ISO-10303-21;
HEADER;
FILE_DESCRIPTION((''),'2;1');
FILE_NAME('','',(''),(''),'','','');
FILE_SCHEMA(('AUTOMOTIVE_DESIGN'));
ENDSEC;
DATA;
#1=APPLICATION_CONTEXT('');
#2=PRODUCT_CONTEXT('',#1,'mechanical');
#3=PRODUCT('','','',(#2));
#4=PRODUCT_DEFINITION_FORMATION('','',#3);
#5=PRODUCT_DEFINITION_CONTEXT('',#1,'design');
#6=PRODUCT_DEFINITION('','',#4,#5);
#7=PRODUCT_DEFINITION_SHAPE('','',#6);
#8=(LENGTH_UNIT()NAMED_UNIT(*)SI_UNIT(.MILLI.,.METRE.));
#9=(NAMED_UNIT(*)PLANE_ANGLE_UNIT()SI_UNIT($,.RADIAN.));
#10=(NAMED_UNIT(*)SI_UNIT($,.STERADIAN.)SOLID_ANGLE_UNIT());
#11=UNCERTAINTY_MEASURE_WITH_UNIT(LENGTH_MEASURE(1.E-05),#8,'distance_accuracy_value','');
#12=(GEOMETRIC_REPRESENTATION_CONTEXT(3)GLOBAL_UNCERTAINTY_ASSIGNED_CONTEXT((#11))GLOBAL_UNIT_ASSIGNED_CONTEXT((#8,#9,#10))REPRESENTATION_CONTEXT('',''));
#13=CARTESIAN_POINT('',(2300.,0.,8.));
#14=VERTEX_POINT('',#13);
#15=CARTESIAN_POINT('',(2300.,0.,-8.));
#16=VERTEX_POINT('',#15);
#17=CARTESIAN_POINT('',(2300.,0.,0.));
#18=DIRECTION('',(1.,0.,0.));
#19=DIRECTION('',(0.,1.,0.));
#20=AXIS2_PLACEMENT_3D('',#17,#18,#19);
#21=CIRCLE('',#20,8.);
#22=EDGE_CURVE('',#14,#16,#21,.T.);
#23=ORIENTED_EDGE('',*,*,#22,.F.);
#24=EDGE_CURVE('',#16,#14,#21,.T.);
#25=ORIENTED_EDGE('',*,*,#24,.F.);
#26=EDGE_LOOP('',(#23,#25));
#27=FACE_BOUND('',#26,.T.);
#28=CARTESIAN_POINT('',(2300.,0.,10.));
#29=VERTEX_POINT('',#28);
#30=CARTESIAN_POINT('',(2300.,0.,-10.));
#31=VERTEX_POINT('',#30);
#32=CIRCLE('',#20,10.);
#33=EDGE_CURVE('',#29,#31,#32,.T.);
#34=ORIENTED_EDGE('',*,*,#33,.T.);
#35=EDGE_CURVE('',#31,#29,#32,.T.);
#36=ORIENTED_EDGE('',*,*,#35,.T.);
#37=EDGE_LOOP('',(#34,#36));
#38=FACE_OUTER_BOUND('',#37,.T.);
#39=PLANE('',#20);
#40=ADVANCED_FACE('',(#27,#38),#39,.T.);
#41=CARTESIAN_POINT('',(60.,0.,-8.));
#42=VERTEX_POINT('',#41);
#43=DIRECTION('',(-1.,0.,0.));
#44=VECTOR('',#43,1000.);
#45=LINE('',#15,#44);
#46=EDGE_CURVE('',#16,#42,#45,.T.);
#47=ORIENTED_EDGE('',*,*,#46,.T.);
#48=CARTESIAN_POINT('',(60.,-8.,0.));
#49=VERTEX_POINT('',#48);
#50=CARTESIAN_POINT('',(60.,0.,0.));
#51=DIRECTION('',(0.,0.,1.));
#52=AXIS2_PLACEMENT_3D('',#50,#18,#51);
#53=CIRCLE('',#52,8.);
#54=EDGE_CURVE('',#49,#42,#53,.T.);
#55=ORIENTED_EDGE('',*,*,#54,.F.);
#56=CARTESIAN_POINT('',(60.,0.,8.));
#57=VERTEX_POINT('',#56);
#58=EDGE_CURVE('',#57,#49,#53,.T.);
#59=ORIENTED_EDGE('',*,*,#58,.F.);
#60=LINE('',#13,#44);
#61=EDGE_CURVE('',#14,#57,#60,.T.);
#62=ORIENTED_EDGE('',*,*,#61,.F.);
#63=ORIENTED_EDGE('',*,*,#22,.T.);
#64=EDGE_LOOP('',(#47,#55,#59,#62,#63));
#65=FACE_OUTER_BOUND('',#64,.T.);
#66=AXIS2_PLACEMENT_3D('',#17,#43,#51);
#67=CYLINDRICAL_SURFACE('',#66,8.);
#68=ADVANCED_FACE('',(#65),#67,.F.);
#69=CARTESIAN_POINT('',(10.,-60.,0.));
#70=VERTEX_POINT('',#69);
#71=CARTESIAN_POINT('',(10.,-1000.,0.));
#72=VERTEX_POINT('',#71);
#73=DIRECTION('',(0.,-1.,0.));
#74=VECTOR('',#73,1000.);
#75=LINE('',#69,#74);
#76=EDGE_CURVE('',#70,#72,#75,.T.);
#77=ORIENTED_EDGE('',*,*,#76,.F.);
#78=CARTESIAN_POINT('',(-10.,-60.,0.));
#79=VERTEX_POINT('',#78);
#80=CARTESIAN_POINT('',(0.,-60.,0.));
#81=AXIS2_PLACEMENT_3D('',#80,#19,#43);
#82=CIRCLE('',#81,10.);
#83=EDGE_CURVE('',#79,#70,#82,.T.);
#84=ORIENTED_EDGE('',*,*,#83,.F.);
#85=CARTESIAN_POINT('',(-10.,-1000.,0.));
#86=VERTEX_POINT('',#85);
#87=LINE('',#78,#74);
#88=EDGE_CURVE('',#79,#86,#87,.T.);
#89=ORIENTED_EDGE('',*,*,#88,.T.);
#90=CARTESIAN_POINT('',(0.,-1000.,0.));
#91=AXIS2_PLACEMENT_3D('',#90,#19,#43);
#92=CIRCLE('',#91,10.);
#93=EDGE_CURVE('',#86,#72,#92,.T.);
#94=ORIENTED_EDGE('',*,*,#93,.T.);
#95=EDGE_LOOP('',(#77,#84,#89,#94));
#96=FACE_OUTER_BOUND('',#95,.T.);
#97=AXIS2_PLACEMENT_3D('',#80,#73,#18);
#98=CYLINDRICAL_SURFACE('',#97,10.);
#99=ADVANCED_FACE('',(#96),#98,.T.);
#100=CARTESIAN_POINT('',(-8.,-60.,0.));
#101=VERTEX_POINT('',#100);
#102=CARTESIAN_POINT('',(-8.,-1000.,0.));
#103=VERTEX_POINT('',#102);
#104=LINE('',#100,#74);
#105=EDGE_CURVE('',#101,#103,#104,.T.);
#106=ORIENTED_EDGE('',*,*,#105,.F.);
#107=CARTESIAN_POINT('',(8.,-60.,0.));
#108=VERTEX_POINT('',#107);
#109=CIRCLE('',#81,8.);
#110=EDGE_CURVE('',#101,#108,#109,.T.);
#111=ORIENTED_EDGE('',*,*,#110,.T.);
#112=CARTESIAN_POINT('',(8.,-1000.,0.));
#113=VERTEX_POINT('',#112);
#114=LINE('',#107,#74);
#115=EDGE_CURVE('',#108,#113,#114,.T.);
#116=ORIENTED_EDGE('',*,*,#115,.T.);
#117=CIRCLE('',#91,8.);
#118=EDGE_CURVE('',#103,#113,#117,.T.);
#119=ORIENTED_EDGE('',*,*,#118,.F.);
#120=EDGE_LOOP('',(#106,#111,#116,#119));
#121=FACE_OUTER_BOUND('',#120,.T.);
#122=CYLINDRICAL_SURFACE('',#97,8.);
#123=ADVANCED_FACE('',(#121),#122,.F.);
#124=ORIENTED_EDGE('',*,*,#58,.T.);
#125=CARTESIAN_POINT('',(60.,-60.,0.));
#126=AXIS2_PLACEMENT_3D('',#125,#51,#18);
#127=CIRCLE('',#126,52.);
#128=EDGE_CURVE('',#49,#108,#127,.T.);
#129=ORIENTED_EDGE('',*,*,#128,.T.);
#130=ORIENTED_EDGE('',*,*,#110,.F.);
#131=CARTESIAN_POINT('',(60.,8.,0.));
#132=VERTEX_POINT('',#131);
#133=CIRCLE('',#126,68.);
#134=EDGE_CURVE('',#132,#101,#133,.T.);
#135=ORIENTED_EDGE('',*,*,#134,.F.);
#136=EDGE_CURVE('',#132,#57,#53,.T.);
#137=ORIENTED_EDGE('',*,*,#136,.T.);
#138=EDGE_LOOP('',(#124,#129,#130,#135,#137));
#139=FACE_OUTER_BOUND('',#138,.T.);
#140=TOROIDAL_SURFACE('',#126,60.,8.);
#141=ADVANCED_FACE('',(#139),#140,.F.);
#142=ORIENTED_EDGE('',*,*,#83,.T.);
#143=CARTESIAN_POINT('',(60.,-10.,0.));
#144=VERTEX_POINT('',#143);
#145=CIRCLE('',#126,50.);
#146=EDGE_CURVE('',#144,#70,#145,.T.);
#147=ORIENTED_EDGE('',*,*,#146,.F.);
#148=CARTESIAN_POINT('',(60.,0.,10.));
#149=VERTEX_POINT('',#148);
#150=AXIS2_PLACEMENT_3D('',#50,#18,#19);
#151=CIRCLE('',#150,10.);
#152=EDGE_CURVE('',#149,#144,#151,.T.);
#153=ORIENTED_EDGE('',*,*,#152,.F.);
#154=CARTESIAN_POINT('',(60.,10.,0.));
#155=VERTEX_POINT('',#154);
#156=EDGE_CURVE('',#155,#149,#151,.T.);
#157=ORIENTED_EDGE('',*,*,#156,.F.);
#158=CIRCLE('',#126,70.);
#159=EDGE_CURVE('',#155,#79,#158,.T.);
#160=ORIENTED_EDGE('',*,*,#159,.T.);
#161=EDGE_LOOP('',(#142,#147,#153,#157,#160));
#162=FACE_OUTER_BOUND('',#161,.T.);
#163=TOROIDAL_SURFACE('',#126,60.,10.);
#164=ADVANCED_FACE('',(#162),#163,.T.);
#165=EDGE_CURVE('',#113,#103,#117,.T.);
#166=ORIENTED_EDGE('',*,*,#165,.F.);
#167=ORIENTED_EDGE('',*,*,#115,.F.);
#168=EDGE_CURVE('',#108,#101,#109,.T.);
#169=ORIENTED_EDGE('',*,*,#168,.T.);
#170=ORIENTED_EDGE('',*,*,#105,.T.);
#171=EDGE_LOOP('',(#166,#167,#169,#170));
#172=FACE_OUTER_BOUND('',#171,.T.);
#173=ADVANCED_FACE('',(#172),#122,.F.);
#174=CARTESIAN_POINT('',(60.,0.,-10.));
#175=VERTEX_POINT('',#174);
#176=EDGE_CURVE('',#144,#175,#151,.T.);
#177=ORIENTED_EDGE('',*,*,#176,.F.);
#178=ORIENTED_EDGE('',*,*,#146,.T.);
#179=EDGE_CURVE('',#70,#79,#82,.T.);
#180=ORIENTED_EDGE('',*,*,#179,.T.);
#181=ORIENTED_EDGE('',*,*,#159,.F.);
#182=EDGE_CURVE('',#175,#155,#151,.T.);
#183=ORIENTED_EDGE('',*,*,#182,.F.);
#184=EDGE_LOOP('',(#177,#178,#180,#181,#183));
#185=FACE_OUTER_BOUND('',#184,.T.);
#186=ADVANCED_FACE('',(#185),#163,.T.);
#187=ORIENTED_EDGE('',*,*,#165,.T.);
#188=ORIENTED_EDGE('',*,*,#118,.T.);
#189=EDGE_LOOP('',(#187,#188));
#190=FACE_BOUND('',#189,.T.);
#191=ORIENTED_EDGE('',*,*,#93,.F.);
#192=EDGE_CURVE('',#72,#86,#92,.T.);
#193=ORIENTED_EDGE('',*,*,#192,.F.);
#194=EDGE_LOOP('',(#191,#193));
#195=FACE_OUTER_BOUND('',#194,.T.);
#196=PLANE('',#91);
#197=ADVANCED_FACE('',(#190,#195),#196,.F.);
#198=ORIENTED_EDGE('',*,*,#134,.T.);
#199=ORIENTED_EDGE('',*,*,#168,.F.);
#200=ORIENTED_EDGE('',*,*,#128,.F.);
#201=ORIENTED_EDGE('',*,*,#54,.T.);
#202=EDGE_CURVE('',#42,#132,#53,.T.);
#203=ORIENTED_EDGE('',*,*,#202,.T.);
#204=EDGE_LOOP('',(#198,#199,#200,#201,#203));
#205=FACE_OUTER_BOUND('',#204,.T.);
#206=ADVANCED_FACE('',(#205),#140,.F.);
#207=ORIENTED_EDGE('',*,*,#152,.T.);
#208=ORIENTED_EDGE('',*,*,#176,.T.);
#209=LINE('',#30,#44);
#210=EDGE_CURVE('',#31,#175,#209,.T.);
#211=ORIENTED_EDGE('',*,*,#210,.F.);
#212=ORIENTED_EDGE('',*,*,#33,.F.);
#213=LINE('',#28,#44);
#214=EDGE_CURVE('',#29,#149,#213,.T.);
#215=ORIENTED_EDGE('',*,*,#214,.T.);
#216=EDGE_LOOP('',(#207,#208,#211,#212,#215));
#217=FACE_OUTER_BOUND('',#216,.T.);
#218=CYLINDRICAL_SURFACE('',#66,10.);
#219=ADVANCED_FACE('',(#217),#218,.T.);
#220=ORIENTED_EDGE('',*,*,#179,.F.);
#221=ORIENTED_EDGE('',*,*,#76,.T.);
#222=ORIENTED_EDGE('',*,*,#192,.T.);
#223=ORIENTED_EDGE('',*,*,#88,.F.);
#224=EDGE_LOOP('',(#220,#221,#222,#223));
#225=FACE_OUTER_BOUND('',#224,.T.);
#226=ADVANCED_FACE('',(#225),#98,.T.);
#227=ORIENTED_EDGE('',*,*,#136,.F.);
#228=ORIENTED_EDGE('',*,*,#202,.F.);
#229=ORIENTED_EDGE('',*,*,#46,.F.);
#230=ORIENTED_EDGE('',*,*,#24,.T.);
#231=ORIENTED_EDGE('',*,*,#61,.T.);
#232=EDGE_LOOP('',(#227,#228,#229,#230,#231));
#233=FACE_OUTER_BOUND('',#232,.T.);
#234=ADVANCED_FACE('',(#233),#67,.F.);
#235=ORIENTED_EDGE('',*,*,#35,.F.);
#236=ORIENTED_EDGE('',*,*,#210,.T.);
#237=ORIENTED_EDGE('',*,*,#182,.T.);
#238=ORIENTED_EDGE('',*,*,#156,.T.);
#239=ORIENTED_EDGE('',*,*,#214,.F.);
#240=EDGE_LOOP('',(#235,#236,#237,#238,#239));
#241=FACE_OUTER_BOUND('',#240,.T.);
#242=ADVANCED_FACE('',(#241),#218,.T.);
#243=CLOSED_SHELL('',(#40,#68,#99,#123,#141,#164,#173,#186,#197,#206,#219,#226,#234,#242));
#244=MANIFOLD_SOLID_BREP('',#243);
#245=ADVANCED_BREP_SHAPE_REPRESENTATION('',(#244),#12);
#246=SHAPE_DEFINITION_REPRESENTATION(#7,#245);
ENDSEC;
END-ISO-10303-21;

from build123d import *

# Parameters (mm, degrees)
SWEEP_THIN1_PROFILE_R   = 10
SWEEP_THIN1_PROFILE_R_2 = 8


with BuildPart() as part:
    # Sweep-Thin1: sweep along a path in Sketch1
    with BuildLine(Plane.XY) as sweep_thin1_path:
        Line((2300, 0), (60, 0))
        ThreePointArc((60, 0), (17.573593129, -17.573593129), (0, -60))
        Line((0, -60), (0, -1000))
    # Sweep-Thin1 profile (on start of the path) → Sweep-Thin1 (sweep)
    with BuildSketch(Plane(origin=(2300, 0, 0), x_dir=(0, 0, -1), z_dir=(-1, 0, 0))):
        Circle(SWEEP_THIN1_PROFILE_R)
        Circle(SWEEP_THIN1_PROFILE_R_2, mode=Mode.SUBTRACT)
    sweep(path=sweep_thin1_path.line)


solid = part.part
